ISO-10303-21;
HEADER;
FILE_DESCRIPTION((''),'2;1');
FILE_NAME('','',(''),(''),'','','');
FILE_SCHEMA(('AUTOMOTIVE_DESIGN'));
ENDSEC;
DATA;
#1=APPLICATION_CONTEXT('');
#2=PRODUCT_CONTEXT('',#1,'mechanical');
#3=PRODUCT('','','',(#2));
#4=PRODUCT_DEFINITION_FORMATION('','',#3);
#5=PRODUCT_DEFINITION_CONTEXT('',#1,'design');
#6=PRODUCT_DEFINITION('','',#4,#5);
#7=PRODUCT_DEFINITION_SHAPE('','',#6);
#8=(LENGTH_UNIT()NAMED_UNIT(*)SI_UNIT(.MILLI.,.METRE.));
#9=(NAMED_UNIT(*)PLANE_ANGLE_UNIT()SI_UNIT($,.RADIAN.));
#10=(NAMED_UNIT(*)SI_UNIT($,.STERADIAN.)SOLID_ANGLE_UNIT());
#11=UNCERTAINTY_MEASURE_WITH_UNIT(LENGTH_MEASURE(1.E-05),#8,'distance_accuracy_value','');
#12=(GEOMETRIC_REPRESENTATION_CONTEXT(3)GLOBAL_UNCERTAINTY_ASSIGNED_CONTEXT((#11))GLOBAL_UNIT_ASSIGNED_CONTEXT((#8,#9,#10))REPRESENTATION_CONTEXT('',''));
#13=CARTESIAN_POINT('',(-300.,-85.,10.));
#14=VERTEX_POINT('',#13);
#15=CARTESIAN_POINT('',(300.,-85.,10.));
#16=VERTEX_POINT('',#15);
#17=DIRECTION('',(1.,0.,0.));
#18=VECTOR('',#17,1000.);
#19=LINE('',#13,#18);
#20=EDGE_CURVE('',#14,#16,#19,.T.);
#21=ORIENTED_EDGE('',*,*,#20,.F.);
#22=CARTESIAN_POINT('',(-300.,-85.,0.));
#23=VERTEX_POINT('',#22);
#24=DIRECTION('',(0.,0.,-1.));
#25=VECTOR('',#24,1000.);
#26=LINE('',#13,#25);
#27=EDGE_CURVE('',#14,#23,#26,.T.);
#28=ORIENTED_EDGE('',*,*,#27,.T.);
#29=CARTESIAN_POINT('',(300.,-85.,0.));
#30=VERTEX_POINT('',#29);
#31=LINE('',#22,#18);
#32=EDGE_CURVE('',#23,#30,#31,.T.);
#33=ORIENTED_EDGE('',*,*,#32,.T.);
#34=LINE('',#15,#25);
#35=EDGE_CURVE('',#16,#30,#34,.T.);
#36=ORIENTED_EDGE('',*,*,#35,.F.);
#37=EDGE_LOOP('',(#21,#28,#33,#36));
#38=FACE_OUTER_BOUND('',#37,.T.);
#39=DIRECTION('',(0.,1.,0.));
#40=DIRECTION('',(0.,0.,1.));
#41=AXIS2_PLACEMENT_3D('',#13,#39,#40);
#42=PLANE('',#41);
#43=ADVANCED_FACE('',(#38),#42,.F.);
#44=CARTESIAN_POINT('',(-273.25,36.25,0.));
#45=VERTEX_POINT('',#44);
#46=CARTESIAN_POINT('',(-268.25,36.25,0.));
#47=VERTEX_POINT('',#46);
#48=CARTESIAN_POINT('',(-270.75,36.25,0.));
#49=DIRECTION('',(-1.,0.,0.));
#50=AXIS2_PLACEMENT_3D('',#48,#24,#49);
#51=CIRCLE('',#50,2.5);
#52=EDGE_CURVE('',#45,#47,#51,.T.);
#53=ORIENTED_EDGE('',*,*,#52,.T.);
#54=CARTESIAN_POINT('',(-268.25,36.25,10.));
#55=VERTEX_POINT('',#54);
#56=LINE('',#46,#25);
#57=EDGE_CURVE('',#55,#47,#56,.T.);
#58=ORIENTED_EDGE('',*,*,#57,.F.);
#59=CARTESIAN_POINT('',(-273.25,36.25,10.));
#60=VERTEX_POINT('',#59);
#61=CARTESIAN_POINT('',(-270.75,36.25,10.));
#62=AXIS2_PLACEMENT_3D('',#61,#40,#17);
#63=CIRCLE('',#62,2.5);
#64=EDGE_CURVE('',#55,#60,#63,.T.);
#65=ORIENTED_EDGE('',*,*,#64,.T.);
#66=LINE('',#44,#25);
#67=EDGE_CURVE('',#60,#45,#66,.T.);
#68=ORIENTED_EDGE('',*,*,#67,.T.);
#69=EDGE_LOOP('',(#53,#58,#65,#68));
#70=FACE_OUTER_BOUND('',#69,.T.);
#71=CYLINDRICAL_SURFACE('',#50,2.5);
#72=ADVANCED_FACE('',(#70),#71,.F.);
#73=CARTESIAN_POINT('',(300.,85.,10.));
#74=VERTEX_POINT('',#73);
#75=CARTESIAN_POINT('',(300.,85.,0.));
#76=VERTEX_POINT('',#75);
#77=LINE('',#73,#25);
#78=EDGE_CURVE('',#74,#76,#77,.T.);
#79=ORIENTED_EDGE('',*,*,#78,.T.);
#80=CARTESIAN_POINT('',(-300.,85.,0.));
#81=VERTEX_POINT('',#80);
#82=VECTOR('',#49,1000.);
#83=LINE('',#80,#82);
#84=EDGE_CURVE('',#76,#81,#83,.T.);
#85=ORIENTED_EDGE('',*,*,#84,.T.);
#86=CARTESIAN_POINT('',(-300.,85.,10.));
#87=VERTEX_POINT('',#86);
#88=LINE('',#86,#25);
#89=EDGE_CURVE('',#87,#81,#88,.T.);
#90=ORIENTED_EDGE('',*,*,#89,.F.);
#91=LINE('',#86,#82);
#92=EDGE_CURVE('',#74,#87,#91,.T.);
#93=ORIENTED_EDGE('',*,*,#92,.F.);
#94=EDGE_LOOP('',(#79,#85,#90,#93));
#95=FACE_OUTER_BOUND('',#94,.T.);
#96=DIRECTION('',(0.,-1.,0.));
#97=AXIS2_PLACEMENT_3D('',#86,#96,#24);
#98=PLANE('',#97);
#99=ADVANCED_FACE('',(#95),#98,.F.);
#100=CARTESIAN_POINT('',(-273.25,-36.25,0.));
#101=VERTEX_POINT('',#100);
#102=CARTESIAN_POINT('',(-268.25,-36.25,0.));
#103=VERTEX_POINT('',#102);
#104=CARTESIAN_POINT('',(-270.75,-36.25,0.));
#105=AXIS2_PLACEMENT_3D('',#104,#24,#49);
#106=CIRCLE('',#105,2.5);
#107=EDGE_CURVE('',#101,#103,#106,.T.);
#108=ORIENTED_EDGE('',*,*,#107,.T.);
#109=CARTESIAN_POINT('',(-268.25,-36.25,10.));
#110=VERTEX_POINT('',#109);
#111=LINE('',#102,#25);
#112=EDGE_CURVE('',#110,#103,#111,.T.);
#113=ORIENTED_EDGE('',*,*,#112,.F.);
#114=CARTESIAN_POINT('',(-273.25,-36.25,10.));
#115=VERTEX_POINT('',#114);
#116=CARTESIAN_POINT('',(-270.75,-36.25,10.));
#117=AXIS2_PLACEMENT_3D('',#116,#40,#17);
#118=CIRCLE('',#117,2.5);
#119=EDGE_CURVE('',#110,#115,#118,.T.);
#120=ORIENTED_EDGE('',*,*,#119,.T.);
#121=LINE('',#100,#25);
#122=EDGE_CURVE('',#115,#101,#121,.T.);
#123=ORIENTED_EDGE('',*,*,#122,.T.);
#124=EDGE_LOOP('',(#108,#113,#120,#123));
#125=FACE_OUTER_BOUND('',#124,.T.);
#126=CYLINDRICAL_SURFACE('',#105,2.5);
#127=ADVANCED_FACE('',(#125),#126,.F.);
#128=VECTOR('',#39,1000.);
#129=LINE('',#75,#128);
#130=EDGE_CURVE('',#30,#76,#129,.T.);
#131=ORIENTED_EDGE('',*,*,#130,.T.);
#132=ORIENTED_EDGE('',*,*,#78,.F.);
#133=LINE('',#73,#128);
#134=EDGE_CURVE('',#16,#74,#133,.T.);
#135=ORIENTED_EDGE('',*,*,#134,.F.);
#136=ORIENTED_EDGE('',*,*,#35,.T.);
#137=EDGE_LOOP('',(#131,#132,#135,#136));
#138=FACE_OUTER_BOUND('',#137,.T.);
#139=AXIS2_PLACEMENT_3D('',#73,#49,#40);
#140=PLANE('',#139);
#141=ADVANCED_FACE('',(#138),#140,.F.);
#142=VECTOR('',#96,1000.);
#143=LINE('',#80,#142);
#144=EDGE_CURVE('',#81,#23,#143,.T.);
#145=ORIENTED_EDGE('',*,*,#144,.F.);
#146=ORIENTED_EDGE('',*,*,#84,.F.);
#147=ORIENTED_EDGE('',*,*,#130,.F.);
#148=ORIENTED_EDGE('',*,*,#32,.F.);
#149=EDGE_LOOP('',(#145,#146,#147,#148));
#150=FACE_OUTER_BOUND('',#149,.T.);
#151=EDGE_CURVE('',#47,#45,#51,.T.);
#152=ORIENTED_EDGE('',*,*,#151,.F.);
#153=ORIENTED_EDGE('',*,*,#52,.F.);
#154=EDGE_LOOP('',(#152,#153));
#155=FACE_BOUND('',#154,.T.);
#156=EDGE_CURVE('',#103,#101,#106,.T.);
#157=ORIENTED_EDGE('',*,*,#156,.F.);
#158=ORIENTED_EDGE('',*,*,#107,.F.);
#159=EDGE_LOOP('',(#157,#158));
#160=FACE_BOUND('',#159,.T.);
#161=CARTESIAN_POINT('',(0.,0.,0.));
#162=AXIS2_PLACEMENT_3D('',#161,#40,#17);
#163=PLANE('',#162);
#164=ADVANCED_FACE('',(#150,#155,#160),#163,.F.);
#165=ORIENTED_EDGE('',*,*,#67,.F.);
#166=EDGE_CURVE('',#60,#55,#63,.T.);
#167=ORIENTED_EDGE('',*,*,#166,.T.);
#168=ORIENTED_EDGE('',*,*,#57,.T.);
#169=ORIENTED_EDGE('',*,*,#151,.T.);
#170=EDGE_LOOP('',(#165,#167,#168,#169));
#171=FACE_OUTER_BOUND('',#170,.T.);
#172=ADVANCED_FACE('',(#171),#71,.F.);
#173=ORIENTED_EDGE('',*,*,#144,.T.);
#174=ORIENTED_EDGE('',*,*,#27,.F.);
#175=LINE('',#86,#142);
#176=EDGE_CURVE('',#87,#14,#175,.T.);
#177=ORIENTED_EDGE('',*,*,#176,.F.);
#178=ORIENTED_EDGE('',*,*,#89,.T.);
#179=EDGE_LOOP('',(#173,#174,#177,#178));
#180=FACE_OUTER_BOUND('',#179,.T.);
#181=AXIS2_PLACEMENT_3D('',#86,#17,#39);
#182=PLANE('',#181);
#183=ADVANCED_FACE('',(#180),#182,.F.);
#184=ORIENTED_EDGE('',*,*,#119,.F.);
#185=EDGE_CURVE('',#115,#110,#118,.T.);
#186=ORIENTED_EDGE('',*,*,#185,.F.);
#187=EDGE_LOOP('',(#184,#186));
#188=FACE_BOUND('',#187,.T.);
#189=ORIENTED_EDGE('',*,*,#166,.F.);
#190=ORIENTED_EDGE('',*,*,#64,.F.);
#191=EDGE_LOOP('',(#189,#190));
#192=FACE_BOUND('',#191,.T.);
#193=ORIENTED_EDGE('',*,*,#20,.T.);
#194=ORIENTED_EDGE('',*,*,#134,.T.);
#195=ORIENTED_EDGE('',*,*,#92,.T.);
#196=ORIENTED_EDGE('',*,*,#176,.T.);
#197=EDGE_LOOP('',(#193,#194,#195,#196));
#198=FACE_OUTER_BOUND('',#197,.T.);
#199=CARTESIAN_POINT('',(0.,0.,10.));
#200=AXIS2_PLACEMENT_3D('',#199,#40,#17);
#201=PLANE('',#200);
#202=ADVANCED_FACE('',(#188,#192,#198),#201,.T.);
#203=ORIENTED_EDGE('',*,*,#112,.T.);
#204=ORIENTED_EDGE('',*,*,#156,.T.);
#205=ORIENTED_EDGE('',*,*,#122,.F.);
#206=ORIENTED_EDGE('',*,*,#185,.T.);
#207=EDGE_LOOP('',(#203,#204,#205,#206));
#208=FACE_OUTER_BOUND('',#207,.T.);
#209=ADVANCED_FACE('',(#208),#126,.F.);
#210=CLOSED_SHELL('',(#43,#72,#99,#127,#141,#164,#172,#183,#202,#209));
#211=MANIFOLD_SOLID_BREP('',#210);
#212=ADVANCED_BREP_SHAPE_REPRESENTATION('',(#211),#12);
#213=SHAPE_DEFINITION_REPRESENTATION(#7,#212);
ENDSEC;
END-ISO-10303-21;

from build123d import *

# Parameters (mm, degrees)
SKETCH1_W             = 600
SKETCH1_H             = 170
BOSS_EXTRUDE1_DEPTH   = 10
M6_TAPPED_HOLE1_D     = 5
M6_TAPPED_HOLE1_DEPTH = 15
M6_TAPPED_HOLE1_TIP   = 1.502151548


with BuildPart() as part:
    # Sketch1 → Boss-Extrude1 (new body)
    with BuildSketch(Plane.XY):
        Rectangle(SKETCH1_W, SKETCH1_H)
    extrude(amount=BOSS_EXTRUDE1_DEPTH)

    # M6 Tapped Hole1
    with Locations(Plane(origin=(0, 0, 0), x_dir=(-1, 0, 0), z_dir=(0, 0, -1))):
        with Locations((270.75, 36.25), (270.75, -36.25)):
            Hole(M6_TAPPED_HOLE1_D / 2, depth=M6_TAPPED_HOLE1_DEPTH)
            with Locations((0, 0, -(M6_TAPPED_HOLE1_DEPTH + M6_TAPPED_HOLE1_TIP / 2))):  # 118° drill point
                Cone(0, M6_TAPPED_HOLE1_D / 2, M6_TAPPED_HOLE1_TIP, mode=Mode.SUBTRACT)


solid = part.part
